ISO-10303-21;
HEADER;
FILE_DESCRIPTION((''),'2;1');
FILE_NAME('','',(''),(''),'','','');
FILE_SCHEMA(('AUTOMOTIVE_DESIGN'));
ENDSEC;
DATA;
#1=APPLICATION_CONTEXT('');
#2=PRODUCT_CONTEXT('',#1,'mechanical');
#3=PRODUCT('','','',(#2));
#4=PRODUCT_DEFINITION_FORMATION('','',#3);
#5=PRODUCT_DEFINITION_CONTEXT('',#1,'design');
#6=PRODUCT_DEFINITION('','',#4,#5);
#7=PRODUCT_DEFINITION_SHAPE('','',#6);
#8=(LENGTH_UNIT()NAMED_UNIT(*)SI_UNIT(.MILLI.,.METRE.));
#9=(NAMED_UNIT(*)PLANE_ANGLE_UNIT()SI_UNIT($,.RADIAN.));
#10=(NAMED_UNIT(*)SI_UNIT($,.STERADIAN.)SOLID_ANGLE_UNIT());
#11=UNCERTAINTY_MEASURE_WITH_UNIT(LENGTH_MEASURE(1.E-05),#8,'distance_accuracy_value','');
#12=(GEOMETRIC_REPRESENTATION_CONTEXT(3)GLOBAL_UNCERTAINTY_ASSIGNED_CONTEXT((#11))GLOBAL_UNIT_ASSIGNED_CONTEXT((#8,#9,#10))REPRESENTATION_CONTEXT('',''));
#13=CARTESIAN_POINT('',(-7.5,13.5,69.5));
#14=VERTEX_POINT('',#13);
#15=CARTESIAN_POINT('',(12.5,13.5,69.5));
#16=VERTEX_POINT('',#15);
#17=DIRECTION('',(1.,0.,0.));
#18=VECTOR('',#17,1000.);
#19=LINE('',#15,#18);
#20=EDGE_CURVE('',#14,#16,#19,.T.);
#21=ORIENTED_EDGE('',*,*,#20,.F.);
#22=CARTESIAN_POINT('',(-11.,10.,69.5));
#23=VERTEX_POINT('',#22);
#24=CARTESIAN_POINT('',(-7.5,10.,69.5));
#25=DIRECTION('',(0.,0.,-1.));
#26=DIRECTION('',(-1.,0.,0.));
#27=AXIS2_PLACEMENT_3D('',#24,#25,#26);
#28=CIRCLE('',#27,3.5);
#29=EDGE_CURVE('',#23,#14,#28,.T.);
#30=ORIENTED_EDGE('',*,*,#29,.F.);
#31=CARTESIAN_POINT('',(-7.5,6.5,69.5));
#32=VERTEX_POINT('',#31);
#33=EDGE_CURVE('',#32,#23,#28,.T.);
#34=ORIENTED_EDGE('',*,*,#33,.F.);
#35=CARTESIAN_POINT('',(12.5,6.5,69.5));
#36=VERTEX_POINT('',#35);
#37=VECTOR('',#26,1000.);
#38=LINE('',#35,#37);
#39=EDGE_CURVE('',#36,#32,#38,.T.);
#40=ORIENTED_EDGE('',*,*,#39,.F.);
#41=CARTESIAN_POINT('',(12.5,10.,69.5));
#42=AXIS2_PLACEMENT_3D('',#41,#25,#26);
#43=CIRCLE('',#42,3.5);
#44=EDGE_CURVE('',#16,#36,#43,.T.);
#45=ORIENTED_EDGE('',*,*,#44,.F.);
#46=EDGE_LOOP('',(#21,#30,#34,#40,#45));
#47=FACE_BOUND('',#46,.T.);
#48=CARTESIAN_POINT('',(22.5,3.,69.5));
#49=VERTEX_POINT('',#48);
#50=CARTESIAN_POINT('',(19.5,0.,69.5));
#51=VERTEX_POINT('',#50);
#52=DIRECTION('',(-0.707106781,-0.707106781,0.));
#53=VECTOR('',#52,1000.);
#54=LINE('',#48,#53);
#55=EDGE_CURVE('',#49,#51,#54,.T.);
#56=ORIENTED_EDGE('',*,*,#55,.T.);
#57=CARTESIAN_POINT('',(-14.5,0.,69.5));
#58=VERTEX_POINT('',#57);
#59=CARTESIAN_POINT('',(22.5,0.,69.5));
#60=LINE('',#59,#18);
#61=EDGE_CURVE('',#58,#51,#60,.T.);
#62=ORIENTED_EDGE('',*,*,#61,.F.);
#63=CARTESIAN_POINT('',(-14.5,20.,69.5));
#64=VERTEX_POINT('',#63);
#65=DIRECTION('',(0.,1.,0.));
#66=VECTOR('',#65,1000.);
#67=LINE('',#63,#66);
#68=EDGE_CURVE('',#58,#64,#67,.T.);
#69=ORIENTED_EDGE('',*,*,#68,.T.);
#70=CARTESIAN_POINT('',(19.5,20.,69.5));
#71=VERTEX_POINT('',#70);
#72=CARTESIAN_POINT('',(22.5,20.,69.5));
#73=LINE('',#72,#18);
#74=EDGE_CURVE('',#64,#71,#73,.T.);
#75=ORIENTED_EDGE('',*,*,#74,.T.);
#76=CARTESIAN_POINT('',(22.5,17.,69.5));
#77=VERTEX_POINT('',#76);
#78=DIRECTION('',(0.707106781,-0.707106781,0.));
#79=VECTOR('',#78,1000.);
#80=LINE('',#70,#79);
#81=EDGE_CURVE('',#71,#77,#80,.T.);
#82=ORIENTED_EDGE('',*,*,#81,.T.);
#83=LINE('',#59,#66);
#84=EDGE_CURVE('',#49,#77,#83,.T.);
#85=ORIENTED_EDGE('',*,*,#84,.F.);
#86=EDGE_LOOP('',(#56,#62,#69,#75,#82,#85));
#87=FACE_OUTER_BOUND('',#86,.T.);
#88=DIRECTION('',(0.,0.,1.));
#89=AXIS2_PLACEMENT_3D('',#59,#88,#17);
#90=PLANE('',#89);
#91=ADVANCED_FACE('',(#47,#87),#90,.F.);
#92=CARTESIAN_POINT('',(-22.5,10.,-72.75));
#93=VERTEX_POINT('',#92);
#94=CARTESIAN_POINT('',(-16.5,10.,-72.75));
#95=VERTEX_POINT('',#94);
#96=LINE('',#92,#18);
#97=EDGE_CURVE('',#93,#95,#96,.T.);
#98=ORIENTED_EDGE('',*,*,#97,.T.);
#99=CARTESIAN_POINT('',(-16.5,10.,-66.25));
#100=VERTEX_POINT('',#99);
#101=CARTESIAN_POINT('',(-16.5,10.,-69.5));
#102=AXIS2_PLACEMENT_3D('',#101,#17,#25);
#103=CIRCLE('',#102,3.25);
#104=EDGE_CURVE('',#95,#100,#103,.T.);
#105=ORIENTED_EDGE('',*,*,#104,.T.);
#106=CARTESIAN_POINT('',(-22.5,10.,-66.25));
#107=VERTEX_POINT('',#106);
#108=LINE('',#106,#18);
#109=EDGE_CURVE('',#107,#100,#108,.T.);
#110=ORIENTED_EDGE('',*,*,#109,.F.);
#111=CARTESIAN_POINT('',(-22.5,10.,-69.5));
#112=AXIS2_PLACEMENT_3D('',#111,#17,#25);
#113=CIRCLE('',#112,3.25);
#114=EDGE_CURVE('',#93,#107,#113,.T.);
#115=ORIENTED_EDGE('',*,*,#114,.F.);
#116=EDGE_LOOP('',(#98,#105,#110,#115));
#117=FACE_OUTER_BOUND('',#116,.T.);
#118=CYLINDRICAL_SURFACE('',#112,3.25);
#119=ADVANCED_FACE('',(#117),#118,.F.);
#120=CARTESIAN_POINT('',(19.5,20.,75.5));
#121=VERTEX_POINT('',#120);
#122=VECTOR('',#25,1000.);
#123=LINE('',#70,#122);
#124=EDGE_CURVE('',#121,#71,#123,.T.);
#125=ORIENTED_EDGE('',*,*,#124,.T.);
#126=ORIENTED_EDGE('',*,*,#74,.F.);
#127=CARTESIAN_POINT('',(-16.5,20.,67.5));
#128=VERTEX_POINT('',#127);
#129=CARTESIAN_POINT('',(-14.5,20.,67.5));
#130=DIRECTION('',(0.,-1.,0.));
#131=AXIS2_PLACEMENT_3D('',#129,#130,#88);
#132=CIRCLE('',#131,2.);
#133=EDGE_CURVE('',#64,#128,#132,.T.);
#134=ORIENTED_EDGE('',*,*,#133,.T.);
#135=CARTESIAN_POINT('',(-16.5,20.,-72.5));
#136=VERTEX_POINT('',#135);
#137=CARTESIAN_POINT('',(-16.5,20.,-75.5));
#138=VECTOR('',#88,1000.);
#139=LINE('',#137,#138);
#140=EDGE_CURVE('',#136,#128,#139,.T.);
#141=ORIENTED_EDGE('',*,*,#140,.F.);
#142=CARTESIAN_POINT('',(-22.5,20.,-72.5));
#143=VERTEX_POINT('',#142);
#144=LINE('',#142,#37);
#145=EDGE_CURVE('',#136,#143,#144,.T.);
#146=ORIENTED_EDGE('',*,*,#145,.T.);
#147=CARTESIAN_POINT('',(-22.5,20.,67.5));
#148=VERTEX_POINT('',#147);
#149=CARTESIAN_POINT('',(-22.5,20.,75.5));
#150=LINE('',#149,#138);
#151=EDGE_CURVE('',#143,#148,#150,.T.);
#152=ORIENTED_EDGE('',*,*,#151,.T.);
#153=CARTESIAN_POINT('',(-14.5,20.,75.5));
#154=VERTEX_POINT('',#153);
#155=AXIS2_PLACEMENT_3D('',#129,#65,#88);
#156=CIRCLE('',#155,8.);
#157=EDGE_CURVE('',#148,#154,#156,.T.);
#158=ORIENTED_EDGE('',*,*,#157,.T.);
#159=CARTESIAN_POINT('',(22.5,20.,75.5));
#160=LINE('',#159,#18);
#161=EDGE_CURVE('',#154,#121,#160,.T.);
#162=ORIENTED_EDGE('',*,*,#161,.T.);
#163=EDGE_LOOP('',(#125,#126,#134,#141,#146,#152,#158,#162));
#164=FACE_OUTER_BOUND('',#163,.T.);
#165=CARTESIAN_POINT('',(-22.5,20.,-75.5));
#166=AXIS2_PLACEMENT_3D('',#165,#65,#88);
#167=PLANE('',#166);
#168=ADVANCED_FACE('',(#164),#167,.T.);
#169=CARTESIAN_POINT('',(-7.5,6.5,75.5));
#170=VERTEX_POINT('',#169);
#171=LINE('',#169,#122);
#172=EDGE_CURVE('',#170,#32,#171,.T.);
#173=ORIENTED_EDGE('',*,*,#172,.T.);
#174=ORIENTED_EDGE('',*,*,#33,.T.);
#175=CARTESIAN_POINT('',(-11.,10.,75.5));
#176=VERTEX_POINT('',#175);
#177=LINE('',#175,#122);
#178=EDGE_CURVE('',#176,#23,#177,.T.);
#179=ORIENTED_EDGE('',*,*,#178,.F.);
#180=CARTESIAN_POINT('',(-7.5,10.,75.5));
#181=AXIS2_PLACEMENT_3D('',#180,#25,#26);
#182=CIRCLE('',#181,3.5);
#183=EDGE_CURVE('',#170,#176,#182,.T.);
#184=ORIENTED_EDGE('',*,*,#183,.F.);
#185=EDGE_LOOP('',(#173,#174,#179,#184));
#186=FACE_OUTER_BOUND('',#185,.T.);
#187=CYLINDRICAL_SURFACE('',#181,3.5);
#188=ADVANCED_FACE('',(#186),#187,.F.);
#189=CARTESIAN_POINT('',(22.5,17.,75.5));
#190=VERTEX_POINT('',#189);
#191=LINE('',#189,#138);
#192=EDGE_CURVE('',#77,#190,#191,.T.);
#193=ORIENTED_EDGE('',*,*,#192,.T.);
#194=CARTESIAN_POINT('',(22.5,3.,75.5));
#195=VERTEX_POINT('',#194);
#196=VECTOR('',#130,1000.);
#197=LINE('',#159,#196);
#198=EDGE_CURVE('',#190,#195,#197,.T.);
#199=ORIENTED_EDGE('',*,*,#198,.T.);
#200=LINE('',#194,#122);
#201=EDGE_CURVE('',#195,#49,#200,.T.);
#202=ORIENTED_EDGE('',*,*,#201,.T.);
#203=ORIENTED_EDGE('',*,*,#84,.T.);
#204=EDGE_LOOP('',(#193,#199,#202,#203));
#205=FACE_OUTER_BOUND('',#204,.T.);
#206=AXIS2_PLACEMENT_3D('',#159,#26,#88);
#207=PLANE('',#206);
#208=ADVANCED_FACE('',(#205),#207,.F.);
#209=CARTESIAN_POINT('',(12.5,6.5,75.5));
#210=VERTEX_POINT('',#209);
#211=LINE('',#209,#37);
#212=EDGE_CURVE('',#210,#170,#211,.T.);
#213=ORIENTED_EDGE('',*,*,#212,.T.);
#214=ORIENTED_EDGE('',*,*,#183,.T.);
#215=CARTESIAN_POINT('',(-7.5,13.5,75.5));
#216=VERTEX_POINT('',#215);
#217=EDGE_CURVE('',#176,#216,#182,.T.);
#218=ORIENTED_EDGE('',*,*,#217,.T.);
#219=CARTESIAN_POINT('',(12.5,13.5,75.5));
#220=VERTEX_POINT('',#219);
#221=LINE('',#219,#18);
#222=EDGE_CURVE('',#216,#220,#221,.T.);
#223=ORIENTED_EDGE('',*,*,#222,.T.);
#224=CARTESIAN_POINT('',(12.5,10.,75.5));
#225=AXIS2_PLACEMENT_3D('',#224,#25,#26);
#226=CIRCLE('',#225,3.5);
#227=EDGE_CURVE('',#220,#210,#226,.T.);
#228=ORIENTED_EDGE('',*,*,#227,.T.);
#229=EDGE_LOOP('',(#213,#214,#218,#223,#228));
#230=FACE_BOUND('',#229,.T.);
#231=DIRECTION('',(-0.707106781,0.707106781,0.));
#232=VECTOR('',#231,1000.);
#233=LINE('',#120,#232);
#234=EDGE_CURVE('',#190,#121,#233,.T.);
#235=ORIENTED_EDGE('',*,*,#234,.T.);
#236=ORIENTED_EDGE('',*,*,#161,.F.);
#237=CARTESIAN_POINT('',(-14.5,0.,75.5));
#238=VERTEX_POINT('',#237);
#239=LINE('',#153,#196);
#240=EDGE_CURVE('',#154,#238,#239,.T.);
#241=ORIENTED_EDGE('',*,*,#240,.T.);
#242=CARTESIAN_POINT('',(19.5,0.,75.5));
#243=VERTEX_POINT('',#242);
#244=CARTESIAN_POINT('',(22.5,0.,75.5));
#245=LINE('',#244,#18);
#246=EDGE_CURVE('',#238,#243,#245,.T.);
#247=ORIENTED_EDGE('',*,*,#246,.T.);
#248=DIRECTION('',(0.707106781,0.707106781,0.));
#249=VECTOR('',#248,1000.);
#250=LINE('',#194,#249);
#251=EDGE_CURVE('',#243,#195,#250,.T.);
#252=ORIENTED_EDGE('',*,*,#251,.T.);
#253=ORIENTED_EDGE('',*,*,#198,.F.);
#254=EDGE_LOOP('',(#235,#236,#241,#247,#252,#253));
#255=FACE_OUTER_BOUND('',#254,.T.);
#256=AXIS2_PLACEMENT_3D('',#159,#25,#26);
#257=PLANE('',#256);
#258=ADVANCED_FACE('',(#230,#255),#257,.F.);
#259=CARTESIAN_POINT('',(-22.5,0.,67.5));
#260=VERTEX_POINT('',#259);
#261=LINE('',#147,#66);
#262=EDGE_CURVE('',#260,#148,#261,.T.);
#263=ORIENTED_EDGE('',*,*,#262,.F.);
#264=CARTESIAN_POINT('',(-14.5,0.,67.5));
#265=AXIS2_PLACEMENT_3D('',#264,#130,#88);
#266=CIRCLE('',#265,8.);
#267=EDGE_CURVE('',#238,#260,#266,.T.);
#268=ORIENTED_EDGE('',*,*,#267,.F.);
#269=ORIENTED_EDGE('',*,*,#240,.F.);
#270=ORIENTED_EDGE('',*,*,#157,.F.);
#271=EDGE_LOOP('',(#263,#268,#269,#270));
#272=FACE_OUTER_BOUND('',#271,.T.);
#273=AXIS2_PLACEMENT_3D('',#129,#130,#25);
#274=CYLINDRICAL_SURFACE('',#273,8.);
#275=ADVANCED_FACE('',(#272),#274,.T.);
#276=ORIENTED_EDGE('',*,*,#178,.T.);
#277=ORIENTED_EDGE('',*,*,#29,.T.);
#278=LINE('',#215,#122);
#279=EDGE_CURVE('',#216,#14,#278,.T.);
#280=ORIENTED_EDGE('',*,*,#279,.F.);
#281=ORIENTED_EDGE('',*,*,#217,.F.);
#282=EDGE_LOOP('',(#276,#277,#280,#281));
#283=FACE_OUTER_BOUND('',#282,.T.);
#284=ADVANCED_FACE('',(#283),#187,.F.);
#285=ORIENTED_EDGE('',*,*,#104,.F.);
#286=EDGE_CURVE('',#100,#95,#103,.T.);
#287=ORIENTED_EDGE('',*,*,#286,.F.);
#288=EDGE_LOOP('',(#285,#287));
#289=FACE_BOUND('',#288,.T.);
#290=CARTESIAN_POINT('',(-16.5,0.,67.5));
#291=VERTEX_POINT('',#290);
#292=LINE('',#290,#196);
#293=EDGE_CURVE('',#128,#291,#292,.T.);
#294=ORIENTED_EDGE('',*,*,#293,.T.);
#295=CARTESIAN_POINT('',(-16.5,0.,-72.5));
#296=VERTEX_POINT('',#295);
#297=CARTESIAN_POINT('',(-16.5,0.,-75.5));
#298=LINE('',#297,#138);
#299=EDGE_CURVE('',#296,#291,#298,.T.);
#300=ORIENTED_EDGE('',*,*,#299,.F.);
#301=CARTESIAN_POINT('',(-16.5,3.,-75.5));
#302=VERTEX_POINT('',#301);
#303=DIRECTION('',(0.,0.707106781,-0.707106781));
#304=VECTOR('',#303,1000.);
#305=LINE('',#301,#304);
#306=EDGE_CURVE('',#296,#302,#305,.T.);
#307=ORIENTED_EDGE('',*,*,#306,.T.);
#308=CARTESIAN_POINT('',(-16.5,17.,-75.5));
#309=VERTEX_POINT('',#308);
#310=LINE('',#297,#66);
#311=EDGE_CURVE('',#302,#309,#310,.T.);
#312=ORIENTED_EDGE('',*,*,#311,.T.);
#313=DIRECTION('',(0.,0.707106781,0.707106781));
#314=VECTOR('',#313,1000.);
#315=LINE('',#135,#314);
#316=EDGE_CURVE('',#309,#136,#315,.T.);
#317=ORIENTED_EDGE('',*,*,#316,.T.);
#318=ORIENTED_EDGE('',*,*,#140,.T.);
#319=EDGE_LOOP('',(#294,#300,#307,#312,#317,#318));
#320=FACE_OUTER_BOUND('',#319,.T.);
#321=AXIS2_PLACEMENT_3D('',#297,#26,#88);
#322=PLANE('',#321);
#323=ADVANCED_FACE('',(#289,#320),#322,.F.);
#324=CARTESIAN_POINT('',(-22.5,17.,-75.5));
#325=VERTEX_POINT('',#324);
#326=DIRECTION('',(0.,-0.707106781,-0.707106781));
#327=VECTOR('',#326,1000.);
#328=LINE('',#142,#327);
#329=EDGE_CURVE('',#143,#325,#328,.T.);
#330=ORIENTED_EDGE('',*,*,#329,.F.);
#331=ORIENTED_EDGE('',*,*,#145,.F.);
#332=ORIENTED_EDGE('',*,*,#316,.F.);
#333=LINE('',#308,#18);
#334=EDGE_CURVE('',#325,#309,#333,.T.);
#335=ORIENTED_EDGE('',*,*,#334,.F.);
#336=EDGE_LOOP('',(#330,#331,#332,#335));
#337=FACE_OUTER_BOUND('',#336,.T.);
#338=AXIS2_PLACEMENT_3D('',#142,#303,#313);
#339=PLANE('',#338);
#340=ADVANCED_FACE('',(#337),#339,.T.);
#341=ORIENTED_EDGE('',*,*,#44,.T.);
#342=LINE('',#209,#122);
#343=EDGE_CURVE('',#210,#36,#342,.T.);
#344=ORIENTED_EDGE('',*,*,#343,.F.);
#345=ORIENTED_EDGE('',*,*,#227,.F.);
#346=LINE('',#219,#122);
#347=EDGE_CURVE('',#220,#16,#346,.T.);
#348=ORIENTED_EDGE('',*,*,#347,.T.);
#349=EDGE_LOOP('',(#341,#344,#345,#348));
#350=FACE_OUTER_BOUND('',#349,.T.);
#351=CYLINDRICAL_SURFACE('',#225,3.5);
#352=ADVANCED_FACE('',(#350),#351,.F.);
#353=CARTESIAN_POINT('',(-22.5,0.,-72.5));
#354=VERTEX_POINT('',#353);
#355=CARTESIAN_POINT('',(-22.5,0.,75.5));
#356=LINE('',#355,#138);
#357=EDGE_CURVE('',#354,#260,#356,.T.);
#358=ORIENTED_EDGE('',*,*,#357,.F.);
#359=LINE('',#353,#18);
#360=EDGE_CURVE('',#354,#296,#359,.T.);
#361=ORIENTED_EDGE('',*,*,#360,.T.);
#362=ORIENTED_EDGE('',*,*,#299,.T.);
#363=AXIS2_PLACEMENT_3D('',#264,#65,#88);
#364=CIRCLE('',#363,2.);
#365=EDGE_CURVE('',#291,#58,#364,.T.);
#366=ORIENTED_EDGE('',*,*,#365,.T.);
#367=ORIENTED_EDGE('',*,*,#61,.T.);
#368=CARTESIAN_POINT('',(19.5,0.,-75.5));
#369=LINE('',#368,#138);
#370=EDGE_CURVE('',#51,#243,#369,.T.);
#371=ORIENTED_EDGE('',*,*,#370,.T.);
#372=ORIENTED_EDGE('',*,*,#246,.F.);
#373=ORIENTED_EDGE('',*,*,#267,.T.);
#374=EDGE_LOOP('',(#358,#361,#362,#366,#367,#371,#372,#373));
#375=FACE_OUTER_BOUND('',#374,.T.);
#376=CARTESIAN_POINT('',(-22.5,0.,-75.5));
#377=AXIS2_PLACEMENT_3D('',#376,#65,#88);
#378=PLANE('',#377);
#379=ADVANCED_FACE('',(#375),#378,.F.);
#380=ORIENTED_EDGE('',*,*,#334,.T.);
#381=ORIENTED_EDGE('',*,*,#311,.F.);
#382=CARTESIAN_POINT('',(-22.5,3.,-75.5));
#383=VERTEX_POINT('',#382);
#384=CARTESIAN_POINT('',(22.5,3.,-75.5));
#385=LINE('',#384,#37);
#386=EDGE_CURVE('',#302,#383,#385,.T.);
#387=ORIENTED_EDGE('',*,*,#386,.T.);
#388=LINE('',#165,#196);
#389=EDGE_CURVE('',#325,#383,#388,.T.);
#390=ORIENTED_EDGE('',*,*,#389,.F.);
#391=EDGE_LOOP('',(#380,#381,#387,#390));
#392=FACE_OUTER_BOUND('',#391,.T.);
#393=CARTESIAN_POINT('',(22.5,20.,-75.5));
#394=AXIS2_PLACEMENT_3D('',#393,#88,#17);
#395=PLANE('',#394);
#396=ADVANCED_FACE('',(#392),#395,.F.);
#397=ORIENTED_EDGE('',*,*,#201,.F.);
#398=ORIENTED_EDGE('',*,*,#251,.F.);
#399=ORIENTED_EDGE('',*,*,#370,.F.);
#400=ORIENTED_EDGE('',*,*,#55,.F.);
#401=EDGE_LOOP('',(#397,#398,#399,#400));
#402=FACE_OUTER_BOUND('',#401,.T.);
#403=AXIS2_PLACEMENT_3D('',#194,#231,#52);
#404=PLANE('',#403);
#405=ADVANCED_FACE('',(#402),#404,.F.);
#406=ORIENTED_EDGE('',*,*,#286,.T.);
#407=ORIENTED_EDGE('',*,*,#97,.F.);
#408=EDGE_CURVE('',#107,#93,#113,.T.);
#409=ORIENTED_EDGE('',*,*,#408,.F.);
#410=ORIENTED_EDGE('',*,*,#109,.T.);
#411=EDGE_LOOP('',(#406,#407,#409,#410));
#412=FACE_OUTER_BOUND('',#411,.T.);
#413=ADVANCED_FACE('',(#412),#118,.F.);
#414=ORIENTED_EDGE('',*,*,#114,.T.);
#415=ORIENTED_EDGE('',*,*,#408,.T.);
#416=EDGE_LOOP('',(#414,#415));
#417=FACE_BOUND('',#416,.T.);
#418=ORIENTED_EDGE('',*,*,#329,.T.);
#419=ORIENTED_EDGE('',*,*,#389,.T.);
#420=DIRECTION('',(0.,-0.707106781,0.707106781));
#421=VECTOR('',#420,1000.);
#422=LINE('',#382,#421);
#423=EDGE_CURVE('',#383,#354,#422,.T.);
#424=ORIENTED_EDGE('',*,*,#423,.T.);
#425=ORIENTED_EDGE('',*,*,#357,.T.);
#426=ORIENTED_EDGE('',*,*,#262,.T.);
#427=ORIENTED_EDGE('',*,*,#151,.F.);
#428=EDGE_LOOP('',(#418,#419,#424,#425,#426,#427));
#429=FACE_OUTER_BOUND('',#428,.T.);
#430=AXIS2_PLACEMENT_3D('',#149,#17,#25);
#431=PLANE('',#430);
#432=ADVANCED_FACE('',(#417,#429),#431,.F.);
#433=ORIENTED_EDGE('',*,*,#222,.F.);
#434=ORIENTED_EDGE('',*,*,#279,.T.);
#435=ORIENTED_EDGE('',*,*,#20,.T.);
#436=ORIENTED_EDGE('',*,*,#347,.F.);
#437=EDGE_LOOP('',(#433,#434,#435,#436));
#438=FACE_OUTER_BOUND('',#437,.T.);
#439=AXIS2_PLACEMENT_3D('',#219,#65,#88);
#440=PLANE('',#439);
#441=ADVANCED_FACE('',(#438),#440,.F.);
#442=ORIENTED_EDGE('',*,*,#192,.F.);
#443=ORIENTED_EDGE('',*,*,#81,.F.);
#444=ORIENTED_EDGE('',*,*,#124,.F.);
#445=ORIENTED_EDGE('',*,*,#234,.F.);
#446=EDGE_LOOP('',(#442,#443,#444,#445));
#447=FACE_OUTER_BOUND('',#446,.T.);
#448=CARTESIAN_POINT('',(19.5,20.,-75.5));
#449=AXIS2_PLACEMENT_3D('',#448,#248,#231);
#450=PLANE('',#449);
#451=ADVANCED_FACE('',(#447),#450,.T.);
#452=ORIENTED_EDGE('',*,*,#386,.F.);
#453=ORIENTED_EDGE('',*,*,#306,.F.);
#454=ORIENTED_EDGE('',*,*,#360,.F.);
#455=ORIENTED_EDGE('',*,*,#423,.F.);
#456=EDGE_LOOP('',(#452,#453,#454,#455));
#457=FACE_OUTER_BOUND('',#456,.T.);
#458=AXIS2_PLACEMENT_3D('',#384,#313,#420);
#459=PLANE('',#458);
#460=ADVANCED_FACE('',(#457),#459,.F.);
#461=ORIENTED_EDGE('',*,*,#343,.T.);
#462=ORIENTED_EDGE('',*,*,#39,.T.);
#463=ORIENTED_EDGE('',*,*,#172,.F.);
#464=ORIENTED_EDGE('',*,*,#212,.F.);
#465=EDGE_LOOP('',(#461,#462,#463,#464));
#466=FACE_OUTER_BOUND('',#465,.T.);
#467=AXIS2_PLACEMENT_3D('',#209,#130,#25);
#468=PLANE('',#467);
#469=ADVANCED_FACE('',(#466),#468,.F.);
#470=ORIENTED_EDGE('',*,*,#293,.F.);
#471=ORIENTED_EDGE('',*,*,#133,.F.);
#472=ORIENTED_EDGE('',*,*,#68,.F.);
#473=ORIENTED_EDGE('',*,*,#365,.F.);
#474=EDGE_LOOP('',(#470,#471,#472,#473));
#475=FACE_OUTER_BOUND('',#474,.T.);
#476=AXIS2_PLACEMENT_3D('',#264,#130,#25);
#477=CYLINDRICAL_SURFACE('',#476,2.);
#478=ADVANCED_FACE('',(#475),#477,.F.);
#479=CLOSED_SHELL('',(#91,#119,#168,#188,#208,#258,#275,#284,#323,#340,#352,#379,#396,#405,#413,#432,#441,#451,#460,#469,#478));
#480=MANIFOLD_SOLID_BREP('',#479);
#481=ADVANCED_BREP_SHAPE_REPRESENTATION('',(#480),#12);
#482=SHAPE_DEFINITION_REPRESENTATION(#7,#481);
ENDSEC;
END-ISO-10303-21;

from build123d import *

# Parameters (mm, degrees)
SKETCH1_W           = 45
SKETCH1_H           = 151
BOSS_EXTRUDE1_DEPTH = 20
SKETCH2_W           = 39
SKETCH2_H           = 145
CUT_EXTRUDE1_DEPTH  = 82.280378936
SKETCH3_R           = 3.25
CUT_EXTRUDE2_DEPTH  = 88.299770905
CUT_EXTRUDE3_DEPTH  = 149.092032196
CHAMFER1_SIZE       = 3
FILLET1_R           = 2
FILLET2_R           = 8


with BuildPart() as part:
    # Sketch1 → Boss-Extrude1 (new body)
    with BuildSketch(Plane(origin=(0, 0, 0), x_dir=(1, 0, 0), z_dir=(0, 1, 0))):
        Rectangle(SKETCH1_W, SKETCH1_H)
    extrude(amount=BOSS_EXTRUDE1_DEPTH)

    # Sketch2 → Cut-Extrude1 (cut, through all)
    with BuildSketch(Plane(origin=(0, 20, 0), x_dir=(1, 0, 0), z_dir=(0, 1, 0))):
        with Locations((3, 3)):
            Rectangle(SKETCH2_W, SKETCH2_H)
    extrude(amount=-CUT_EXTRUDE1_DEPTH, mode=Mode.SUBTRACT)

    # Sketch3 → Cut-Extrude2 (cut, through all)
    with BuildSketch(Plane(origin=(-16.5, 0, 0), x_dir=(0, 0, -1), z_dir=(1, 0, 0))):
        with Locations((69.5, 10)):
            Circle(SKETCH3_R)
    extrude(amount=-CUT_EXTRUDE2_DEPTH, mode=Mode.SUBTRACT)

    # Sketch4 → Cut-Extrude3 (cut, through all)
    with BuildSketch(Plane(origin=(0, 0, 69.5), x_dir=(-1, 0, 0), z_dir=(0, 0, -1))):
        with BuildLine():
            Line((-12.5, 13.5), (7.5, 13.5))
            ThreePointArc((7.5, 13.5), (11, 10), (7.5, 6.5))
            Line((7.5, 6.5), (-12.5, 6.5))
            ThreePointArc((-12.5, 6.5), (-16, 10), (-12.5, 13.5))
        make_face()
    extrude(amount=-CUT_EXTRUDE3_DEPTH, mode=Mode.SUBTRACT)

    # Chamfer1
    chamfer1_edges = [part.edges().sort_by_distance(p)[0] for p in [
        (22.5, 20, 72.5),
        (-19.5, 0, -75.5),
        (-19.5, 20, -75.5),
        (22.5, 0, 72.5),
    ]]
    chamfer(chamfer1_edges, length=CHAMFER1_SIZE)

    # Fillet1
    fillet1_edges = [part.edges().sort_by_distance(p)[0] for p in [
        (-16.5, 10, 69.5),
    ]]
    fillet(fillet1_edges, radius=FILLET1_R)

    # Fillet2
    fillet2_edges = [part.edges().sort_by_distance(p)[0] for p in [
        (-22.5, 10, 75.5),
    ]]
    fillet(fillet2_edges, radius=FILLET2_R)


solid = part.part
